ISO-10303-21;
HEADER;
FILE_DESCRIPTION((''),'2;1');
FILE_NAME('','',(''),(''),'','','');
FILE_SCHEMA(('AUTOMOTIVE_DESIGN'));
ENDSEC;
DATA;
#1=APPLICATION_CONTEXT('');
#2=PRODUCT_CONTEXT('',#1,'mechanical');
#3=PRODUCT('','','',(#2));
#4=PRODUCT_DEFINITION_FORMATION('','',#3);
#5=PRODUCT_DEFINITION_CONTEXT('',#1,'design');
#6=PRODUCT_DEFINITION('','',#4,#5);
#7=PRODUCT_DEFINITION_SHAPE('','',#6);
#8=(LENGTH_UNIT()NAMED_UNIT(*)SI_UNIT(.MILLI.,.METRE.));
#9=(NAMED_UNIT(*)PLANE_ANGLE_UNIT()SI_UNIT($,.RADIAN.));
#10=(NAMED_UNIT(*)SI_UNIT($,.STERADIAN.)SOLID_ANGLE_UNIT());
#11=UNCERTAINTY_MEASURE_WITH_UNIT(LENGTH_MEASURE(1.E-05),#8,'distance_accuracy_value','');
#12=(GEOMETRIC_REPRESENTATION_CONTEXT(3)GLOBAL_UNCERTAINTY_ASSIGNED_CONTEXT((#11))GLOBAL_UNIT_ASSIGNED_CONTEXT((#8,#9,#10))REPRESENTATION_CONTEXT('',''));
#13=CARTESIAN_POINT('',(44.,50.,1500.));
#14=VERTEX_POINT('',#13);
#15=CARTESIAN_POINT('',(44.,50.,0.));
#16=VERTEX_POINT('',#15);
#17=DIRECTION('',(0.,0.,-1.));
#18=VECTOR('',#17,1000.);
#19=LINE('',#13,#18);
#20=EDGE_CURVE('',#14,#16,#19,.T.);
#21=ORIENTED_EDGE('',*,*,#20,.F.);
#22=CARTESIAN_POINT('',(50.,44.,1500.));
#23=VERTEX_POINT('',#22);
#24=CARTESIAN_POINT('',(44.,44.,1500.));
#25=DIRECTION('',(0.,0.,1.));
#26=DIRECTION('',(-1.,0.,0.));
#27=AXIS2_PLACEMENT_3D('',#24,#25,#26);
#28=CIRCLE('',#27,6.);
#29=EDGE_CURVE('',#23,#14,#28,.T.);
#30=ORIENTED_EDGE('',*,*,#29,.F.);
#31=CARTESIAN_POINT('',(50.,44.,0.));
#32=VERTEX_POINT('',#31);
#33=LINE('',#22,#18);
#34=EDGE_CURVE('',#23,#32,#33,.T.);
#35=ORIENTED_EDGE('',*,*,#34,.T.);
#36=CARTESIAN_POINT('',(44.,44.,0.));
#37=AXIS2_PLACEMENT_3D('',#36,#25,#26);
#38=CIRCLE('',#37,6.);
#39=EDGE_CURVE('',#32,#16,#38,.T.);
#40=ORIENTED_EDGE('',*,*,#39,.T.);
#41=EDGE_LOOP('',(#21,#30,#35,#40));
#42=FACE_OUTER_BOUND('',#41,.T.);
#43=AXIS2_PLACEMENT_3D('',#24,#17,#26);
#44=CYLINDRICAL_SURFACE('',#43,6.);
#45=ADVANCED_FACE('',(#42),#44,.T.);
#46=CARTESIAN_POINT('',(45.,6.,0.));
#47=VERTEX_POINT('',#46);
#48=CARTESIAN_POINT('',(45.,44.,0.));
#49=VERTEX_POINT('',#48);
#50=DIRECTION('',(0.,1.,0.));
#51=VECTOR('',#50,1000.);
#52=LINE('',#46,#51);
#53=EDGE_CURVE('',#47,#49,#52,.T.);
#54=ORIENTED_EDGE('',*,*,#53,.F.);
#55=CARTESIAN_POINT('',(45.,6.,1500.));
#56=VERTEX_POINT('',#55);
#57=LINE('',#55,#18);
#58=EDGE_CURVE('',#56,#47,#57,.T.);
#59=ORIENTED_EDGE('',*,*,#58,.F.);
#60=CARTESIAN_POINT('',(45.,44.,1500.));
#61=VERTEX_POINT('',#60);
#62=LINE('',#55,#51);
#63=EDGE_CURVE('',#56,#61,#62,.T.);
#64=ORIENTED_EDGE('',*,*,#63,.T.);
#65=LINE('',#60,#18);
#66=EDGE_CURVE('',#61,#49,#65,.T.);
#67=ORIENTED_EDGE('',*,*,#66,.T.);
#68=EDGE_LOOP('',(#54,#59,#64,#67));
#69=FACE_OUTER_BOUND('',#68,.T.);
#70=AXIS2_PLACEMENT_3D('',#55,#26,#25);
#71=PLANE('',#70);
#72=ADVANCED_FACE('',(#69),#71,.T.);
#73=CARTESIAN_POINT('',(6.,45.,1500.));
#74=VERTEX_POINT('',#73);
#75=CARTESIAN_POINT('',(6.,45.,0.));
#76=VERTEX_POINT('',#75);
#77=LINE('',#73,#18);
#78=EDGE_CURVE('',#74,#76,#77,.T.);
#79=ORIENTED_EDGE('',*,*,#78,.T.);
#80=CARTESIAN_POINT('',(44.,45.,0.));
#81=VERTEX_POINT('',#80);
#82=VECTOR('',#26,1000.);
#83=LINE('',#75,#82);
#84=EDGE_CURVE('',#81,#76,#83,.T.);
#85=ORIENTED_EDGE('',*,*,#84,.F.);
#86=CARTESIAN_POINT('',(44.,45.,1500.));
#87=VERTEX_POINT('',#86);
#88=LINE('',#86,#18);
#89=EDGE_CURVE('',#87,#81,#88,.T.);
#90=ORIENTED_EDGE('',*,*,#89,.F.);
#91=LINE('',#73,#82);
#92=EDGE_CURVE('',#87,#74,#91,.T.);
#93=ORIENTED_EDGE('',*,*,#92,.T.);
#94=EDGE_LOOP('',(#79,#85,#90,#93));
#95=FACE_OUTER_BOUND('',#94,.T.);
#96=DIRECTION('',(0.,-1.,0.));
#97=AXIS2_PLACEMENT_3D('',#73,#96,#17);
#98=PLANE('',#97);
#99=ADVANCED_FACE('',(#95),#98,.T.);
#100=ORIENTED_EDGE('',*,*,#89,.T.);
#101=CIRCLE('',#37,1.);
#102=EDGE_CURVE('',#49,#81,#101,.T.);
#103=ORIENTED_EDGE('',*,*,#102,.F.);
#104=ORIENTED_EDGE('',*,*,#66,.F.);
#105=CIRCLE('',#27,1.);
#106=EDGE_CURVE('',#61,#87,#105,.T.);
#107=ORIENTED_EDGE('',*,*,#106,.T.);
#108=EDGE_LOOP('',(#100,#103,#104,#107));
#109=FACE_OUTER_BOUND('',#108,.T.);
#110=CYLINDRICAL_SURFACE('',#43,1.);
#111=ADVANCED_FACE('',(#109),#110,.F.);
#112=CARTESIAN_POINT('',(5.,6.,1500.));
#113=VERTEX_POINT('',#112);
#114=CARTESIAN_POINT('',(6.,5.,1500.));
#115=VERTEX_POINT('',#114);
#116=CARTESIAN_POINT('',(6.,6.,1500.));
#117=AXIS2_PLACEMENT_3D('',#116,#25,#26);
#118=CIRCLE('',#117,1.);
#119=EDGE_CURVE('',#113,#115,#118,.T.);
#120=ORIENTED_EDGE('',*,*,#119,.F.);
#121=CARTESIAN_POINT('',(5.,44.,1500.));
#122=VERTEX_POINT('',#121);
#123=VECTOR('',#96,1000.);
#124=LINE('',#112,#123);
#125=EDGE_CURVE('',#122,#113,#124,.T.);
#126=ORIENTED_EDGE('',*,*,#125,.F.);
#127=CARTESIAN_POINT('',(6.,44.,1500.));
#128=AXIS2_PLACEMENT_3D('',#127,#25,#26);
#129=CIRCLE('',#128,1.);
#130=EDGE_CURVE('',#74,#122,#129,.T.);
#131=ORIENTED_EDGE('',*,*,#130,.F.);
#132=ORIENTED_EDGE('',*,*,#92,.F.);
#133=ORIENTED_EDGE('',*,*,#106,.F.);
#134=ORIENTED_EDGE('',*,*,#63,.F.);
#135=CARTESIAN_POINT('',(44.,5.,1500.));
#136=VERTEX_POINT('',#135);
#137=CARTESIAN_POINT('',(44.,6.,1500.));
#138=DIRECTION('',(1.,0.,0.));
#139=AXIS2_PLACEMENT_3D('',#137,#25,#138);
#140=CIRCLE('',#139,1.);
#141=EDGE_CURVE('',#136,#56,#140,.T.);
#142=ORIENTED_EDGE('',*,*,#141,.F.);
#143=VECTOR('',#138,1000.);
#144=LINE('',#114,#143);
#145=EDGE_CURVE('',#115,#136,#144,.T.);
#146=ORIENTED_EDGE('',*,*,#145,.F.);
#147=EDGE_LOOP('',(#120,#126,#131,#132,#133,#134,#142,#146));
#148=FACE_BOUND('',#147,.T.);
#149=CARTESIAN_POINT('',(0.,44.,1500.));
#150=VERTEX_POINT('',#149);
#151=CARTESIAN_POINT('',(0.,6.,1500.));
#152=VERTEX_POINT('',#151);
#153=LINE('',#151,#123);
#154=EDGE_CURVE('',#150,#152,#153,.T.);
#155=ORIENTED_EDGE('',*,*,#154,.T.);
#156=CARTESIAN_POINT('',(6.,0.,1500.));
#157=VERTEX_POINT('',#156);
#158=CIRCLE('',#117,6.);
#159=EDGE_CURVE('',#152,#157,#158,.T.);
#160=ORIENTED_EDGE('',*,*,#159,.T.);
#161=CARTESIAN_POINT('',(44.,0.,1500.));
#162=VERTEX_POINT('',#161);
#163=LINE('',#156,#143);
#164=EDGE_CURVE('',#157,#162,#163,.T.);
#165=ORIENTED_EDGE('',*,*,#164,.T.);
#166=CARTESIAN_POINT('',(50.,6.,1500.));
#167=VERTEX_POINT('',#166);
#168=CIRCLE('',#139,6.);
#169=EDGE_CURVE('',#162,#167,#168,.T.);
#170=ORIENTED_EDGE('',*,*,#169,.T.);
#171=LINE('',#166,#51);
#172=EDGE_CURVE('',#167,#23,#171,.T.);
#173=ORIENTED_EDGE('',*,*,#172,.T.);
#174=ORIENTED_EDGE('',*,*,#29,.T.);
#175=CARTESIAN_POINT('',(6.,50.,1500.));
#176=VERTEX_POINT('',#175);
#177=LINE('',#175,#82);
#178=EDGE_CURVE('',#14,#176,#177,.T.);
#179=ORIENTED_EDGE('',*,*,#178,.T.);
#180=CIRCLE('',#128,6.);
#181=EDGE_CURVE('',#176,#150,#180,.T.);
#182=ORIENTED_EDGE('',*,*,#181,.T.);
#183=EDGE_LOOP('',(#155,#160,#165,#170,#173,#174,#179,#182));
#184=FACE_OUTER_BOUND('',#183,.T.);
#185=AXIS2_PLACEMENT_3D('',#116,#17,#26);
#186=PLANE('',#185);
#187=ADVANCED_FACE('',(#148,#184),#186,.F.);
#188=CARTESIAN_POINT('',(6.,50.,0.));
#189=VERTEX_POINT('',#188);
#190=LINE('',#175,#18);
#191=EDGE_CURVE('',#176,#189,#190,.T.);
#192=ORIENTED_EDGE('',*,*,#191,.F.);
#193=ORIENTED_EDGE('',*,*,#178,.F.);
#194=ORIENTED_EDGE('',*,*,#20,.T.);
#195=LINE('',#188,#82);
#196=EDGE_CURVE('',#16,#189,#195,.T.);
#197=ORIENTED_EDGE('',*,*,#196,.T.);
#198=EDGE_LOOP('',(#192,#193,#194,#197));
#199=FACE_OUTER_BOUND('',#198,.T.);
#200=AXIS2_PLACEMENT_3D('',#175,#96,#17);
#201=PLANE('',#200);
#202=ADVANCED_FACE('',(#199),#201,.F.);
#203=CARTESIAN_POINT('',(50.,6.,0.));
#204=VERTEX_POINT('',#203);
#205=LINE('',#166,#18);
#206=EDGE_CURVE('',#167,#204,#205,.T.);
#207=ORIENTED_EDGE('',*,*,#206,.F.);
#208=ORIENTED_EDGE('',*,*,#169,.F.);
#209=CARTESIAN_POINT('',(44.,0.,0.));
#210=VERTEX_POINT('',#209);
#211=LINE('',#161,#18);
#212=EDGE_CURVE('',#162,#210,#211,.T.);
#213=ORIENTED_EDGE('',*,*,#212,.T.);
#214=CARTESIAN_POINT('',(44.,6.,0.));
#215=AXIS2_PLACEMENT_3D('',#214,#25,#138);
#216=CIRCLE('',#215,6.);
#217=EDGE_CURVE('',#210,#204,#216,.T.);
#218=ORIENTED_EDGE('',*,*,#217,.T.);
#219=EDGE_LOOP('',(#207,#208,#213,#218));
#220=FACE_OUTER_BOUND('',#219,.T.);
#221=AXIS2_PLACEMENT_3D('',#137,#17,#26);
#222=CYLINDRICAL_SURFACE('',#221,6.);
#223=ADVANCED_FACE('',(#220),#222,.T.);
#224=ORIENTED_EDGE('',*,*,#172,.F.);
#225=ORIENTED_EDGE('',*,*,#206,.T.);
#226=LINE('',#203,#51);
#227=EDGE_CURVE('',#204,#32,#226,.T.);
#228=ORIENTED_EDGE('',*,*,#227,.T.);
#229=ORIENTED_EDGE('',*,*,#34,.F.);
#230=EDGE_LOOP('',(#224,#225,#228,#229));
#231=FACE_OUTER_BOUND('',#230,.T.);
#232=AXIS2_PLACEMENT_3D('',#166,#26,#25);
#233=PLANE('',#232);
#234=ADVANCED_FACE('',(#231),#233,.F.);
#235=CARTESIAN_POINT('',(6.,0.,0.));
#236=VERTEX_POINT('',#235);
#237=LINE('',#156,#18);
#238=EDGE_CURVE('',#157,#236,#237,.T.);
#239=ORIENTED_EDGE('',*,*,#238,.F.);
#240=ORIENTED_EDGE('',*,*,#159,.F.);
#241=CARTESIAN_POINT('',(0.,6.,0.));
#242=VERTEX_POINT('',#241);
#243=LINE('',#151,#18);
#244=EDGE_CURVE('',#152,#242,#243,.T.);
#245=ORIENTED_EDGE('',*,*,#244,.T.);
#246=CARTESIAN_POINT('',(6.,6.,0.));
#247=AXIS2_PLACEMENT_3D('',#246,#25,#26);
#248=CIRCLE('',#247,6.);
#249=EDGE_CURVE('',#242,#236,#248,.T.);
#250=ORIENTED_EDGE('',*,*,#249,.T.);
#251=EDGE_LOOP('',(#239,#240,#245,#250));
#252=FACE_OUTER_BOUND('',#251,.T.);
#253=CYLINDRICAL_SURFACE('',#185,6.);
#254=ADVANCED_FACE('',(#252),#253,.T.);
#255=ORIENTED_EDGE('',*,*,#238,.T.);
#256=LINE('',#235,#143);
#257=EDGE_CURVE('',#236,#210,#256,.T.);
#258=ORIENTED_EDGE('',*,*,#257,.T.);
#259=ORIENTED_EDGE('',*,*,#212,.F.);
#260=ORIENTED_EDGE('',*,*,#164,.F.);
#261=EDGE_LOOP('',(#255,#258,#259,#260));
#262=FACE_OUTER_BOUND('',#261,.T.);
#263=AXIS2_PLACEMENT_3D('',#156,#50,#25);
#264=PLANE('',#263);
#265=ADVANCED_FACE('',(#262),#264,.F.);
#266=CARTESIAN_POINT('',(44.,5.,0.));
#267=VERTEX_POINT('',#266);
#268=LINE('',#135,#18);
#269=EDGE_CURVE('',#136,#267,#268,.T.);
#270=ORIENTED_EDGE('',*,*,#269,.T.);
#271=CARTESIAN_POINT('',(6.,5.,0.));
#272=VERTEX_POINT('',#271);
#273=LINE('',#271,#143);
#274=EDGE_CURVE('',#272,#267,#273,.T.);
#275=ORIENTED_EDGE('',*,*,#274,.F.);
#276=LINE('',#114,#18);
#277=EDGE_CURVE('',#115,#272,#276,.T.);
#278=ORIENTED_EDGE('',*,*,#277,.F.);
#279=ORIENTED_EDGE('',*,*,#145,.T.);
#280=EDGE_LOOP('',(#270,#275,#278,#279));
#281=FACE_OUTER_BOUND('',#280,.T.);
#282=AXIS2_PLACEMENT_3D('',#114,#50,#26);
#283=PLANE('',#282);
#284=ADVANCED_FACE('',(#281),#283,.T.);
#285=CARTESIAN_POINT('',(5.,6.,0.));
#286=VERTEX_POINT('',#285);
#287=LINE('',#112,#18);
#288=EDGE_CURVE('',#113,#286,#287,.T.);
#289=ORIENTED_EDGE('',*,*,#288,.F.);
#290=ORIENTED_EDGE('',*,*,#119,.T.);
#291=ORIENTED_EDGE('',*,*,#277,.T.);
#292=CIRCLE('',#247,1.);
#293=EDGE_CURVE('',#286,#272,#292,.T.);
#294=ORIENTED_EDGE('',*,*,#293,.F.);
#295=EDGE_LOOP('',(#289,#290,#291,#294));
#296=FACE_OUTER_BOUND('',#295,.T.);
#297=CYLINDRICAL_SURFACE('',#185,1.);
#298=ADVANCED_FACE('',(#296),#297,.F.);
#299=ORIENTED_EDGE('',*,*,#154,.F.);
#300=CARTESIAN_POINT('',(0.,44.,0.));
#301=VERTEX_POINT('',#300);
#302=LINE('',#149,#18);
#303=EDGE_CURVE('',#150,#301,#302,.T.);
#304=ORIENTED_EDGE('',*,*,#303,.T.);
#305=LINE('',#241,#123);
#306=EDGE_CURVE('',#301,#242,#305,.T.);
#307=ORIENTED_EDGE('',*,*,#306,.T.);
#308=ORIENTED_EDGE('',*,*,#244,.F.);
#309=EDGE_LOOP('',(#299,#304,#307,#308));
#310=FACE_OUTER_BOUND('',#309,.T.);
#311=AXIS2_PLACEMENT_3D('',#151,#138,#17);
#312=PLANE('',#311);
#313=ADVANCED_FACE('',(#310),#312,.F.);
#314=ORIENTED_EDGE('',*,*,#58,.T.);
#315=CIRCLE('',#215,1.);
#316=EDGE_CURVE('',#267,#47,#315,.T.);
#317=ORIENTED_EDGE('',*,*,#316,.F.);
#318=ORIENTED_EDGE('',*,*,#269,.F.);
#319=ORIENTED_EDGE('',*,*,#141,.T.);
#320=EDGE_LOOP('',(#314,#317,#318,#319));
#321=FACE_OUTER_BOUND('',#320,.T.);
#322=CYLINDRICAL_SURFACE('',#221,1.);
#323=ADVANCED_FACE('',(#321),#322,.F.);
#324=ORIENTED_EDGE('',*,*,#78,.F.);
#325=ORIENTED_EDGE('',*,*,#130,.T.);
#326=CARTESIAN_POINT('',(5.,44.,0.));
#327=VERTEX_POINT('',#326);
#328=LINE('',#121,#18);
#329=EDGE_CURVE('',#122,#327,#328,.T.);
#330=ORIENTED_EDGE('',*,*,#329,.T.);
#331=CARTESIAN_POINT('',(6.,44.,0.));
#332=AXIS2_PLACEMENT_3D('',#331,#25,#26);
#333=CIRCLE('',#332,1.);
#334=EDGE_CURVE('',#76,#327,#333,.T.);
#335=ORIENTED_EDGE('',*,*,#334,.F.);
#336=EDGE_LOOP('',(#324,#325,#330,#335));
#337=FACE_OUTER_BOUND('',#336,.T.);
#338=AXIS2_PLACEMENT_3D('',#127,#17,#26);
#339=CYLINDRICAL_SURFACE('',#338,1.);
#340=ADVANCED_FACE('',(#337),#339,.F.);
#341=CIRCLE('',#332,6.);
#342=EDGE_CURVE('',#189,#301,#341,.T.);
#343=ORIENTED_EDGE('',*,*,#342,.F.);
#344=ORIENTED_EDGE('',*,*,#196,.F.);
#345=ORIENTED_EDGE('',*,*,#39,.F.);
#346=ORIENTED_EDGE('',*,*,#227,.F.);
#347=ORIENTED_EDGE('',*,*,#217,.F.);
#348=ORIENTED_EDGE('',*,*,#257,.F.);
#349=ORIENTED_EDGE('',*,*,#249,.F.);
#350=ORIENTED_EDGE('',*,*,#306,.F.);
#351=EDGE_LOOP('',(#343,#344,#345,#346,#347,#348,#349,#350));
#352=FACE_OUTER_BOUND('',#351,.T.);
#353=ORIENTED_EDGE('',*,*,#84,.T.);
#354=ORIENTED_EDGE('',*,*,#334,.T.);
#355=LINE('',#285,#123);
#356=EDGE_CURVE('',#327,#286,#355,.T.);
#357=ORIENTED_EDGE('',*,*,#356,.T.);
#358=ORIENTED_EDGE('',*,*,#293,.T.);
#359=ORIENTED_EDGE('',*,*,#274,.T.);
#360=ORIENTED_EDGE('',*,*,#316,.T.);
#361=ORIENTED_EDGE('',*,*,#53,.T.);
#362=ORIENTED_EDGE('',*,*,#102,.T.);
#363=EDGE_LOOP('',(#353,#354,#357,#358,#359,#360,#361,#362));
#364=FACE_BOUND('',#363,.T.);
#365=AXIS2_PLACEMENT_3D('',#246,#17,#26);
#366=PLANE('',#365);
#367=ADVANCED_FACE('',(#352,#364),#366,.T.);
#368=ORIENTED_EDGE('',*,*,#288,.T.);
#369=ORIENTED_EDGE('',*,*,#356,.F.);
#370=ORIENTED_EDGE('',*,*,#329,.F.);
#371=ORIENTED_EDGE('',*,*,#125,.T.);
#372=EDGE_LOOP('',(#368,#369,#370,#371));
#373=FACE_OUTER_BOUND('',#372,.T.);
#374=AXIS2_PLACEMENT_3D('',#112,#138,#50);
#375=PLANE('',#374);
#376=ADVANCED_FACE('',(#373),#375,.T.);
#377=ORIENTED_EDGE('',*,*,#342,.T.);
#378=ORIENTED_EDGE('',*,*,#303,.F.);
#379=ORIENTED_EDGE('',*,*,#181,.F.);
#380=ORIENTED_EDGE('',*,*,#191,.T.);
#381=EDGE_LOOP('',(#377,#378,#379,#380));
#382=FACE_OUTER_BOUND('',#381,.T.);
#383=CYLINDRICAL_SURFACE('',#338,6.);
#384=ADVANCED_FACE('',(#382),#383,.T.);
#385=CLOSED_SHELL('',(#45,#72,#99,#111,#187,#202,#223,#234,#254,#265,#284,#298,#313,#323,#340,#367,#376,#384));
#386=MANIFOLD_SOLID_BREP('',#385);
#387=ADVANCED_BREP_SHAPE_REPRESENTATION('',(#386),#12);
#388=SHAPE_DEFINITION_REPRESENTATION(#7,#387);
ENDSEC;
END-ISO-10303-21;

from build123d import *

# Parameters (mm, degrees)
BOSS_EXTRUDE1_DEPTH = 1500


with BuildPart() as part:
    # Sketch1 → Boss-Extrude1 (new body)
    with BuildSketch(Plane.XY):
        with BuildLine():
            Line((6, 0), (44, 0))
            ThreePointArc((44, 0), (48.242640687, 1.757359313), (50, 6))
            Line((50, 6), (50, 44))
            ThreePointArc((50, 44), (48.242640687, 48.242640687), (44, 50))
            Line((44, 50), (6, 50))
            ThreePointArc((6, 50), (1.757359313, 48.242640687), (0, 44))
            Line((0, 44), (0, 6))
            ThreePointArc((0, 6), (1.757359313, 1.757359313), (6, 0))
        make_face()
        with BuildLine():
            Line((6, 45), (44, 45))
            ThreePointArc((44, 45), (44.707106781, 44.707106781), (45, 44))
            Line((45, 44), (45, 6))
            ThreePointArc((45, 6), (44.707106781, 5.292893219), (44, 5))
            Line((44, 5), (6, 5))
            ThreePointArc((6, 5), (5.292893219, 5.292893219), (5, 6))
            Line((5, 6), (5, 44))
            ThreePointArc((5, 44), (5.292893219, 44.707106781), (6, 45))
        make_face(mode=Mode.SUBTRACT)
    extrude(amount=BOSS_EXTRUDE1_DEPTH)


solid = part.part
